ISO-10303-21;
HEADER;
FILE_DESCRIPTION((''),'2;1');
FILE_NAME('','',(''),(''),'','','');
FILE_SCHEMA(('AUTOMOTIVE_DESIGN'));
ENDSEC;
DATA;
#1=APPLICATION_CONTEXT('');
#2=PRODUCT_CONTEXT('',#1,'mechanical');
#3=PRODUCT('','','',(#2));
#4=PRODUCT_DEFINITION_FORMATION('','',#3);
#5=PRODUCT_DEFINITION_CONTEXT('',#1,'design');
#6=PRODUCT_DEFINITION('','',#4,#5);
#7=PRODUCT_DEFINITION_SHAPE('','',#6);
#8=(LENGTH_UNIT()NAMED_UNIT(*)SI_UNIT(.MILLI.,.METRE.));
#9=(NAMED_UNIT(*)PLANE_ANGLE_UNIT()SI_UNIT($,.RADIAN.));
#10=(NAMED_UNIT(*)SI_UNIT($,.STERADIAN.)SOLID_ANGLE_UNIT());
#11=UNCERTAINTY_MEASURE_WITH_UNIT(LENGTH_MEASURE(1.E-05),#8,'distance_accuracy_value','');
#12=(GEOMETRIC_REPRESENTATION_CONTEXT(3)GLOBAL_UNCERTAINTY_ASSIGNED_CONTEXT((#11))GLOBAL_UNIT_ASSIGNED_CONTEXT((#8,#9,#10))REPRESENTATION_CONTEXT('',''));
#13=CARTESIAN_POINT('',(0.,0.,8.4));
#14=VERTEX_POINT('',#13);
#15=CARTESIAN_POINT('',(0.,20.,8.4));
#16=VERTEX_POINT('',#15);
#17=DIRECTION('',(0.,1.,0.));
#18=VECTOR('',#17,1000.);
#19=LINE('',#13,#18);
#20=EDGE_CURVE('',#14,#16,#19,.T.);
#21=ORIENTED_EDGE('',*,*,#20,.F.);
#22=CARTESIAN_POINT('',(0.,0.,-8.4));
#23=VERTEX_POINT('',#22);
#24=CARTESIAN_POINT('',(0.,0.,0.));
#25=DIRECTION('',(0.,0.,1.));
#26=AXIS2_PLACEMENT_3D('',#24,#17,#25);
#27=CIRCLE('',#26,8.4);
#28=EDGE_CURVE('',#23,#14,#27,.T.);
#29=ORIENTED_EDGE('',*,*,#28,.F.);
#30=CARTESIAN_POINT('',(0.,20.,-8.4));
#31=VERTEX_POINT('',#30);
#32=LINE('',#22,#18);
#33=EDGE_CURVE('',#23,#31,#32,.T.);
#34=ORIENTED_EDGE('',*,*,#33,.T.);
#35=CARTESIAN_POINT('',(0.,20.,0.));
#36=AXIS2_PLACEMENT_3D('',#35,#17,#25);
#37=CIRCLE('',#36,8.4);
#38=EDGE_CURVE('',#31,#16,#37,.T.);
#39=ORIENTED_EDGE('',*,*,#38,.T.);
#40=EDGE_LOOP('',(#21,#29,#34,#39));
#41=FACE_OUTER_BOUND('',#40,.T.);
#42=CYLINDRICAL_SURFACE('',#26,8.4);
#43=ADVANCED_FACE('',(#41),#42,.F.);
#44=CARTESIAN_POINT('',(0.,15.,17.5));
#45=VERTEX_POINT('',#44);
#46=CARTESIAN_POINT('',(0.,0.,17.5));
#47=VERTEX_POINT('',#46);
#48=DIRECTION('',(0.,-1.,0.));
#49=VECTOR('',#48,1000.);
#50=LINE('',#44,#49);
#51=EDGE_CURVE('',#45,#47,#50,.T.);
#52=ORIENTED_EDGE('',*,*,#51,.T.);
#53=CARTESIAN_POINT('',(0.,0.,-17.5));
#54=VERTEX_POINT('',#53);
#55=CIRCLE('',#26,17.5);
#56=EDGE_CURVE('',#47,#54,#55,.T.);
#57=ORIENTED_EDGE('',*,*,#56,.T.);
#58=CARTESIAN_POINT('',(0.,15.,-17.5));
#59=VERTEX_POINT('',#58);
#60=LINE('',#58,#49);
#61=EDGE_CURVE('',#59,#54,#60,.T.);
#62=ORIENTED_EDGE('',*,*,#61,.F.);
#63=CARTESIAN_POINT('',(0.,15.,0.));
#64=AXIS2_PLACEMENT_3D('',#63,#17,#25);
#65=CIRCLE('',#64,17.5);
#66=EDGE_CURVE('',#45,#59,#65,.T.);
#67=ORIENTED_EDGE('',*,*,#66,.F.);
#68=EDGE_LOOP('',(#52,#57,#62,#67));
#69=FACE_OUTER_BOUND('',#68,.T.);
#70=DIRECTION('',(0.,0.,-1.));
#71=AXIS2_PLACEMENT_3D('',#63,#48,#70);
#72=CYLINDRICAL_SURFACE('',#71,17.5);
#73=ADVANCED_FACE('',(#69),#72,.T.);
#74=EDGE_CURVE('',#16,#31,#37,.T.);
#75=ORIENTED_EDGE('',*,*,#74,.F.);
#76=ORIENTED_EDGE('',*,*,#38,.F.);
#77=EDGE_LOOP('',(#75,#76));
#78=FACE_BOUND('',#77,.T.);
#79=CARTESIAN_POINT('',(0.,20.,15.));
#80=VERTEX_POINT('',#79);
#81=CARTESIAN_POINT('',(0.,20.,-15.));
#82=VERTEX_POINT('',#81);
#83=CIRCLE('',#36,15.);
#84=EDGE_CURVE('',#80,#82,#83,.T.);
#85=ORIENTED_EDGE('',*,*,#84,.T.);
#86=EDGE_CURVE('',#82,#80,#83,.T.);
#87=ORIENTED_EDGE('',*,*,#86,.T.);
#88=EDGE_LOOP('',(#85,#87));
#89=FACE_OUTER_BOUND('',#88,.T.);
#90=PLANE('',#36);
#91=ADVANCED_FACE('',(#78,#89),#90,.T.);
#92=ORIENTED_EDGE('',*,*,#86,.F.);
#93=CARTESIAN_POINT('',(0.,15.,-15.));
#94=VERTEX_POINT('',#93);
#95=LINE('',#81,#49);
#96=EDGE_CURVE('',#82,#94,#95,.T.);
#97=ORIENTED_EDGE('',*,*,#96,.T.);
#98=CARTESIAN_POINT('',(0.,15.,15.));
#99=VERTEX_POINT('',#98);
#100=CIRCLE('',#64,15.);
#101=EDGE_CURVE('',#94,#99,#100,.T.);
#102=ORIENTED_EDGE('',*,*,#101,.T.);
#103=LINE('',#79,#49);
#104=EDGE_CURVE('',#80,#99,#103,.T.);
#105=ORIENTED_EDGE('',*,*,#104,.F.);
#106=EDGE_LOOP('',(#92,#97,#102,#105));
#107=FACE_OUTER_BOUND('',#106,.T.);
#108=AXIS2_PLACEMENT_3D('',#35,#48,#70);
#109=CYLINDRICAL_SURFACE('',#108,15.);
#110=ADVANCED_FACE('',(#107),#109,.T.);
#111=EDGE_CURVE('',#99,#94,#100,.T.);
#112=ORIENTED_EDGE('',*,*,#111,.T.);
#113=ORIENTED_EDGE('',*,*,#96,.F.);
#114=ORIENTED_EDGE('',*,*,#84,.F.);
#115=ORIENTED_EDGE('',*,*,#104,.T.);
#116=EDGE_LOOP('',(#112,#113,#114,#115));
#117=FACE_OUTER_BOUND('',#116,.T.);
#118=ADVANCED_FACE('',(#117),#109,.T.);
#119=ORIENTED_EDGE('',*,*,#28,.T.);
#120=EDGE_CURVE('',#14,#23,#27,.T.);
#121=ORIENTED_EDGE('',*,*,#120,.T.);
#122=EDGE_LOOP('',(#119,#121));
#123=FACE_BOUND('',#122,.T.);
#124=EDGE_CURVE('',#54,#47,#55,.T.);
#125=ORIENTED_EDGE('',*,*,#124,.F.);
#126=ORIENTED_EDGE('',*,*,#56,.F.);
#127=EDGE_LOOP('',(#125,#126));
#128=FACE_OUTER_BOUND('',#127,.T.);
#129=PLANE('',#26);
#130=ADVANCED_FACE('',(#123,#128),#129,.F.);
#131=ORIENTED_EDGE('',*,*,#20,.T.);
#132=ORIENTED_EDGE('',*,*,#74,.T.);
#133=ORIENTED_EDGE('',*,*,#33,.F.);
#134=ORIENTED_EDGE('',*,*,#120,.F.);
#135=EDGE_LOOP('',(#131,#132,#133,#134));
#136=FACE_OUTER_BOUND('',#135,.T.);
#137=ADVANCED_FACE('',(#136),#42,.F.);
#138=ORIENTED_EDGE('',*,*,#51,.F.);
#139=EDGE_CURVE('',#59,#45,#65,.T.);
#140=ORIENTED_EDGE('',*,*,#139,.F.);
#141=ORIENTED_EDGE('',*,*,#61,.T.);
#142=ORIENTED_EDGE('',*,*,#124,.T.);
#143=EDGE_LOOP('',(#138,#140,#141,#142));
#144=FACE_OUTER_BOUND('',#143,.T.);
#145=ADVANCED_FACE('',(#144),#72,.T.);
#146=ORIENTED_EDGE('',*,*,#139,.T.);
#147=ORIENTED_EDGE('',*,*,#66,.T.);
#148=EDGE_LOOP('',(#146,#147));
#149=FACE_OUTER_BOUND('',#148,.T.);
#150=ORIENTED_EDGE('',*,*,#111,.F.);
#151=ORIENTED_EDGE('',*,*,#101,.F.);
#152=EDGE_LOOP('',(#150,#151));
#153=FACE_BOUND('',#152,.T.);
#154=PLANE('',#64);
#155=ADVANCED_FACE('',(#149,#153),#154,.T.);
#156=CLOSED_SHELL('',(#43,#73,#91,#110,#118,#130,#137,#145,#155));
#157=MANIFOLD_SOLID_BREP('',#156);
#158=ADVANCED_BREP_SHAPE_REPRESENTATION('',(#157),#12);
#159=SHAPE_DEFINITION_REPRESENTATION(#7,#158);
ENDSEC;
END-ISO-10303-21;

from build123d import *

# Parameters (mm, degrees)
SKETCH1_R           = 17.5
BOSS_EXTRUDE1_DEPTH = 15
SKETCH2_R           = 15
BOSS_EXTRUDE2_DEPTH = 5
SKETCH3_R           = 8.4
CUT_EXTRUDE1_DEPTH  = 32.819805153


with BuildPart() as part:
    # Sketch1 → Boss-Extrude1 (new body)
    with BuildSketch(Plane(origin=(0, 0, 0), x_dir=(1, 0, 0), z_dir=(0, 1, 0))):
        with Locations(Location((0, 0, 0), (0, 0, 270))):
            Circle(SKETCH1_R)
    extrude(amount=BOSS_EXTRUDE1_DEPTH)

    # Sketch2 → Boss-Extrude2 (add)
    with BuildSketch(Plane(origin=(0, 15, 0), x_dir=(1, 0, 0), z_dir=(0, 1, 0))):
        with Locations(Location((0, 0, 0), (0, 0, 270))):
            Circle(SKETCH2_R)
    extrude(amount=BOSS_EXTRUDE2_DEPTH)

    # Sketch3 → Cut-Extrude1 (cut, through all)
    with BuildSketch(Plane(origin=(0, 20, 0), x_dir=(1, 0, 0), z_dir=(0, 1, 0))):
        with Locations(Location((0, 0, 0), (0, 0, 270))):
            Circle(SKETCH3_R)
    extrude(amount=-CUT_EXTRUDE1_DEPTH, mode=Mode.SUBTRACT)


solid = part.part
